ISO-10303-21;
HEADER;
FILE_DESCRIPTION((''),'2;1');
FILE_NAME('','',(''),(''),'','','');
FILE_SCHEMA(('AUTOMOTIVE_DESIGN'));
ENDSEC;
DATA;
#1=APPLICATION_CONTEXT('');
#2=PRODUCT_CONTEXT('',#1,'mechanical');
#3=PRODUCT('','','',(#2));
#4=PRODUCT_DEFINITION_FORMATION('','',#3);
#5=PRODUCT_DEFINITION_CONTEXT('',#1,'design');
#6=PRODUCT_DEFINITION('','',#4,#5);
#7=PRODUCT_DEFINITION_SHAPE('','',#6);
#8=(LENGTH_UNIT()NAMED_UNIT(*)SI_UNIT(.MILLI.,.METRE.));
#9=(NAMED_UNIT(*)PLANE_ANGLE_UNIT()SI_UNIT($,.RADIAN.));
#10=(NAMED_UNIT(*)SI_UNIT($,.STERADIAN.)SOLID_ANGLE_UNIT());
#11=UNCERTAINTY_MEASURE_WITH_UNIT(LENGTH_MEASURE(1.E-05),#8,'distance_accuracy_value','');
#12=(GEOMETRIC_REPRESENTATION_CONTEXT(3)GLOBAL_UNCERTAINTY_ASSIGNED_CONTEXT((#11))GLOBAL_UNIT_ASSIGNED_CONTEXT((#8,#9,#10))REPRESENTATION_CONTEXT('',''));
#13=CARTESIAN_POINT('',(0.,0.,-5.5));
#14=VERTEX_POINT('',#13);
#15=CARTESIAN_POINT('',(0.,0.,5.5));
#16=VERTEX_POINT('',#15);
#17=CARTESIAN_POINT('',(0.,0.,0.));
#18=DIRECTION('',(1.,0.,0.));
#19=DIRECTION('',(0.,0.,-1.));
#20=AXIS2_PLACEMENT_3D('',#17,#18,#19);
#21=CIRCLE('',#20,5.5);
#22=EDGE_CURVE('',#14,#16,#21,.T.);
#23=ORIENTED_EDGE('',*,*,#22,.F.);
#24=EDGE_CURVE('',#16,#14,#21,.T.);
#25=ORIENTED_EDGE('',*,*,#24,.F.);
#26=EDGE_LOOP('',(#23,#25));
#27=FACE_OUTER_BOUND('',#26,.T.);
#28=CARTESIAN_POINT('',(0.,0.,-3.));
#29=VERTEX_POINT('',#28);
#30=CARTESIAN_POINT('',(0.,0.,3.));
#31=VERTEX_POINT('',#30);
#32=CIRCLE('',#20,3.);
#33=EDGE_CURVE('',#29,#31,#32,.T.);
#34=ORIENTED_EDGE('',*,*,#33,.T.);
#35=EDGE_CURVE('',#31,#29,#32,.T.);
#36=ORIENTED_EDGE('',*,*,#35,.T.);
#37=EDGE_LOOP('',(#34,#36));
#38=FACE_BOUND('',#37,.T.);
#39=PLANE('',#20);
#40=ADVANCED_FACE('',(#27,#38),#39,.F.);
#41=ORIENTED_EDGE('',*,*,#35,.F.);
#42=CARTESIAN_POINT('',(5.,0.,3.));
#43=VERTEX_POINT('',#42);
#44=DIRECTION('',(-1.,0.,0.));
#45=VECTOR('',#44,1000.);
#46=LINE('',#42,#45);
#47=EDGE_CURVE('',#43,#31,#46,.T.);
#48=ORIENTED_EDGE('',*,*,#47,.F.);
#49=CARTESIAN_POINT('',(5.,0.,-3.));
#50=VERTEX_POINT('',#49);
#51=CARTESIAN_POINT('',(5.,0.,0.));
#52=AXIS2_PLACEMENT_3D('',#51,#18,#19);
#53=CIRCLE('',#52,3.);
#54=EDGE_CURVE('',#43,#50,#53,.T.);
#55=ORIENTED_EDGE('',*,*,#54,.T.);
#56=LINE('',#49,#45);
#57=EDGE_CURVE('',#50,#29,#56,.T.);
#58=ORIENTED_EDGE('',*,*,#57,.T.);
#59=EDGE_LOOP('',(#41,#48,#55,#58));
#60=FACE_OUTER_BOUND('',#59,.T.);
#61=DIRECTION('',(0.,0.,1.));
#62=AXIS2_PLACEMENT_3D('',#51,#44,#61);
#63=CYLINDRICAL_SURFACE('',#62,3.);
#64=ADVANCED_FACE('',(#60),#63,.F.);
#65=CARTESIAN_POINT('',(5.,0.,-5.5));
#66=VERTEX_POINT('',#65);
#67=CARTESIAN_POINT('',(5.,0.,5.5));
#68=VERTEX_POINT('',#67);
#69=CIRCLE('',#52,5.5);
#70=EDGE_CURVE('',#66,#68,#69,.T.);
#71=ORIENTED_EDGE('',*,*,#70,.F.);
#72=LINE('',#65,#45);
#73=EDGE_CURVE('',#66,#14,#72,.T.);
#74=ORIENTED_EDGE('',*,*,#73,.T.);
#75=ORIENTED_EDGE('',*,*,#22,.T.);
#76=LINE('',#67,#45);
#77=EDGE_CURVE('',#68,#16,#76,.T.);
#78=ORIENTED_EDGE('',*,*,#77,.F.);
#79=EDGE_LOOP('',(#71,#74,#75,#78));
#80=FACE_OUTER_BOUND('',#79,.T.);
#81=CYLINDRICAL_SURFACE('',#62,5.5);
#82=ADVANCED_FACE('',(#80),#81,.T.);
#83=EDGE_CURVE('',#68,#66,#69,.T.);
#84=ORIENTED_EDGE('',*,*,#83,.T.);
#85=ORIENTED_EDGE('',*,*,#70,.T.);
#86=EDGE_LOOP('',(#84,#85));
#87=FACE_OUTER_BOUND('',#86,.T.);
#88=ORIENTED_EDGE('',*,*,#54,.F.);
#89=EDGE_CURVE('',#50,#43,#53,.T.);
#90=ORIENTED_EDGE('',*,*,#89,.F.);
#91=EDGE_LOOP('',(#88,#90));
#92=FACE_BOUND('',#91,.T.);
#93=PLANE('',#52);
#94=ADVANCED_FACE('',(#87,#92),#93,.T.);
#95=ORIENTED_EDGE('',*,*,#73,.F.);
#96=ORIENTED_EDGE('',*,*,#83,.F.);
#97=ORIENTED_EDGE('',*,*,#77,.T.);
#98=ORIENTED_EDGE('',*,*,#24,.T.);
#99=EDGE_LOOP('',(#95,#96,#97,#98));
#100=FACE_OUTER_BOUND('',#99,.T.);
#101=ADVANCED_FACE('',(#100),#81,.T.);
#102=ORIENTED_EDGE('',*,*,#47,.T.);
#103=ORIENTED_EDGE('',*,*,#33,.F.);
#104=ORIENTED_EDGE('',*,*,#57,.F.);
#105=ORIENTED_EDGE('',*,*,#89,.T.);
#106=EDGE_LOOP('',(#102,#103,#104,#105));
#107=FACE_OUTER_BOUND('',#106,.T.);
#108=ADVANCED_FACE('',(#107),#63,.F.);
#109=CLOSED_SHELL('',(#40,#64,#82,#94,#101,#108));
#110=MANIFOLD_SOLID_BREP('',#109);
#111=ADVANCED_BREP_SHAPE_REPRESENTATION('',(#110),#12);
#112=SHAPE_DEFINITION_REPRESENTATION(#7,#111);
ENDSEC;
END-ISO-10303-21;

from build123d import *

# Parameters (mm, degrees)
SKETCH1_R           = 5.5
SKETCH1_R_2         = 3
BOSS_EXTRUDE1_DEPTH = 5


with BuildPart() as part:
    # Sketch1 → Boss-Extrude1 (new body)
    with BuildSketch(Plane(origin=(0, 0, 0), x_dir=(0, 0, -1), z_dir=(1, 0, 0))):
        Circle(SKETCH1_R)
        Circle(SKETCH1_R_2, mode=Mode.SUBTRACT)
    extrude(amount=BOSS_EXTRUDE1_DEPTH)


solid = part.part
